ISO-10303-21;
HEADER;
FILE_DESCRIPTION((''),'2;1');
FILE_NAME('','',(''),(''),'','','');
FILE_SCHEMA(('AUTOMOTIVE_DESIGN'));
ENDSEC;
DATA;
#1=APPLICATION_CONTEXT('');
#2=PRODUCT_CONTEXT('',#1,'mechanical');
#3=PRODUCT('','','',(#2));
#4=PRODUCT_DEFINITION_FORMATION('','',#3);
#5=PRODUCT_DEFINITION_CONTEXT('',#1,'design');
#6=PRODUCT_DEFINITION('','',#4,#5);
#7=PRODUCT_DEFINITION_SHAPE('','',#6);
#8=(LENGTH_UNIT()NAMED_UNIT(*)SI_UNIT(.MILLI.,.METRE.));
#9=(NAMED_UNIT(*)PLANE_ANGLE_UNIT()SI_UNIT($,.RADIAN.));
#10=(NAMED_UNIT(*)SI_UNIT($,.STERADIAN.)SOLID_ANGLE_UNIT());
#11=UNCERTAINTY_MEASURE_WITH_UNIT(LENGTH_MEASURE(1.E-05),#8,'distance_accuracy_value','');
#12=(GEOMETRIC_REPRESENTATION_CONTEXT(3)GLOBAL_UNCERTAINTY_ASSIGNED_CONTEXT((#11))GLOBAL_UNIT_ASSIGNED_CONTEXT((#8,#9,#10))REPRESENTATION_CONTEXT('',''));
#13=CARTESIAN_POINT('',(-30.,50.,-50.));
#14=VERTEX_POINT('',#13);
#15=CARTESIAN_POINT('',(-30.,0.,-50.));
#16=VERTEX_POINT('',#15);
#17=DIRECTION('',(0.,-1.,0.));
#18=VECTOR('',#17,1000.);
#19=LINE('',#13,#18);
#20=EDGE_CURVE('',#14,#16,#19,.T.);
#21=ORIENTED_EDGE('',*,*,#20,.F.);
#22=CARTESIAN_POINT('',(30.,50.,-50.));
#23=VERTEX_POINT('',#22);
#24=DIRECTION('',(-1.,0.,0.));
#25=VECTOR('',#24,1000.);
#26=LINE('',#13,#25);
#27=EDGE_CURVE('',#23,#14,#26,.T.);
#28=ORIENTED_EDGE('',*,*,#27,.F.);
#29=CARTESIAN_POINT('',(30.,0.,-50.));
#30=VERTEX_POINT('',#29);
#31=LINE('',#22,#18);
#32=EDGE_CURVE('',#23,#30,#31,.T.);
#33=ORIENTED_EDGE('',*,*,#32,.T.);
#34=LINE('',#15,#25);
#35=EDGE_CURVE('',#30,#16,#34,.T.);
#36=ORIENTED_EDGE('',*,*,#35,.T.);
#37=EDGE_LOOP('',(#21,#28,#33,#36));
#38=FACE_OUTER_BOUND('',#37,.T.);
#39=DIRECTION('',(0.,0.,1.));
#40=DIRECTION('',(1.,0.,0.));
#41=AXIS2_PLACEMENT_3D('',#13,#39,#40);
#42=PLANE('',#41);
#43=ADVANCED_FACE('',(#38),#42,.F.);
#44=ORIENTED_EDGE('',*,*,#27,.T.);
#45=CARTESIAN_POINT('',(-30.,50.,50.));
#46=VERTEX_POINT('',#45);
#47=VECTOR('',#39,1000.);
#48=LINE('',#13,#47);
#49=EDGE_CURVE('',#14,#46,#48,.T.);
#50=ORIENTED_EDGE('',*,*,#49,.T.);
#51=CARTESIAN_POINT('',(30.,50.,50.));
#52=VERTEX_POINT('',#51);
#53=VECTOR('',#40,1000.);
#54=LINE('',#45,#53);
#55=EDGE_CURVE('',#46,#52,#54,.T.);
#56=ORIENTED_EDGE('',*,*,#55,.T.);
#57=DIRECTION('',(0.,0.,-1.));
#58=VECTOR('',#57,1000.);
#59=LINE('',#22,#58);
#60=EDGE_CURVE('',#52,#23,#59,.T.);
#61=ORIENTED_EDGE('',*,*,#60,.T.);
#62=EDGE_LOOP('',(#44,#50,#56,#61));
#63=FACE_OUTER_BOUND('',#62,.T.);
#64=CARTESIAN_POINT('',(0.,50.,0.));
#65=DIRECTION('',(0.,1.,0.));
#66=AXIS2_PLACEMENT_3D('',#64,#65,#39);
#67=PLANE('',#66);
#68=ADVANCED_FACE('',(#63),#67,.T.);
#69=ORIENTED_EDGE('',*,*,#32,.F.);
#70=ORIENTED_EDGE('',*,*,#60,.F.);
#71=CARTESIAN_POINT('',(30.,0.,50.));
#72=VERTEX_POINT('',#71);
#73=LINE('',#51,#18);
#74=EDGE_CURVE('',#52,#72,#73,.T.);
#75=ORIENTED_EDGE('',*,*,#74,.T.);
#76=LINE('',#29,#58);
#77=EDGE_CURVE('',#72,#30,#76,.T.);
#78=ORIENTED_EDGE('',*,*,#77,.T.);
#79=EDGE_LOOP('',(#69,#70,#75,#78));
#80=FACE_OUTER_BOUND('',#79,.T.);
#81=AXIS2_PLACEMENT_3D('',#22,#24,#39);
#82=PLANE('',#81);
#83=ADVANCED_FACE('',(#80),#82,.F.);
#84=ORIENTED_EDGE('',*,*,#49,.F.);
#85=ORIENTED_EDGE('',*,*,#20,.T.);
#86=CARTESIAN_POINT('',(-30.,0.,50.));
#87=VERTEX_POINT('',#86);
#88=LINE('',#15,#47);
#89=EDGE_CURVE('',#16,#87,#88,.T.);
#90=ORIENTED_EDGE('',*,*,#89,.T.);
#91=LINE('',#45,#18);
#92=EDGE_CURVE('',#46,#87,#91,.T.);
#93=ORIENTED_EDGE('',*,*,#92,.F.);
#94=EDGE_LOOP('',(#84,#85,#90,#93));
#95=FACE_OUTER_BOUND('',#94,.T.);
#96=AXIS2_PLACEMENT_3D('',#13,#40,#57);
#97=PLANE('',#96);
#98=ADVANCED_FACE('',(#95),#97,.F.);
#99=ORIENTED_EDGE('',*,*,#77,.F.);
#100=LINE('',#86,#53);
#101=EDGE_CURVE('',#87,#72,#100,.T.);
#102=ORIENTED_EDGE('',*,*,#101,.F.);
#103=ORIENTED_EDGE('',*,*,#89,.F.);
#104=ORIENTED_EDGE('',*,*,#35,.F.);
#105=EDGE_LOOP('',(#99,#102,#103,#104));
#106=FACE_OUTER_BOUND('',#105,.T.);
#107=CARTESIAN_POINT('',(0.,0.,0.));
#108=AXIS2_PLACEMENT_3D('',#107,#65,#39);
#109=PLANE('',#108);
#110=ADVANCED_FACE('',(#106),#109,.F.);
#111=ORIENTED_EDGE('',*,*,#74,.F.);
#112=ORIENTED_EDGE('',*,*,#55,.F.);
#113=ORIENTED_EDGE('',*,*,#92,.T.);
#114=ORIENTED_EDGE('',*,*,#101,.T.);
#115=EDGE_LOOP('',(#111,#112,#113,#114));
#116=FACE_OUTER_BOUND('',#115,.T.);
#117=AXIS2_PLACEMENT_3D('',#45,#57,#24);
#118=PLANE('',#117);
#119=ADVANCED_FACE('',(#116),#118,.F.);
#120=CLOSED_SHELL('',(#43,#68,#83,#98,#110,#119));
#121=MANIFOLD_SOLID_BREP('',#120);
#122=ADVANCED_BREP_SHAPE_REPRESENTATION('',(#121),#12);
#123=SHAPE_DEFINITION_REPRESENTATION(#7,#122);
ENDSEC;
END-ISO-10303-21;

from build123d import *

# Parameters (mm, degrees)
SKETCH1_W           = 60
SKETCH1_H           = 100
BOSS_EXTRUDE1_DEPTH = 50


with BuildPart() as part:
    # Sketch1 → Boss-Extrude1 (new body)
    with BuildSketch(Plane(origin=(0, 0, 0), x_dir=(1, 0, 0), z_dir=(0, 1, 0))):
        Rectangle(SKETCH1_W, SKETCH1_H)
    extrude(amount=BOSS_EXTRUDE1_DEPTH)


solid = part.part
